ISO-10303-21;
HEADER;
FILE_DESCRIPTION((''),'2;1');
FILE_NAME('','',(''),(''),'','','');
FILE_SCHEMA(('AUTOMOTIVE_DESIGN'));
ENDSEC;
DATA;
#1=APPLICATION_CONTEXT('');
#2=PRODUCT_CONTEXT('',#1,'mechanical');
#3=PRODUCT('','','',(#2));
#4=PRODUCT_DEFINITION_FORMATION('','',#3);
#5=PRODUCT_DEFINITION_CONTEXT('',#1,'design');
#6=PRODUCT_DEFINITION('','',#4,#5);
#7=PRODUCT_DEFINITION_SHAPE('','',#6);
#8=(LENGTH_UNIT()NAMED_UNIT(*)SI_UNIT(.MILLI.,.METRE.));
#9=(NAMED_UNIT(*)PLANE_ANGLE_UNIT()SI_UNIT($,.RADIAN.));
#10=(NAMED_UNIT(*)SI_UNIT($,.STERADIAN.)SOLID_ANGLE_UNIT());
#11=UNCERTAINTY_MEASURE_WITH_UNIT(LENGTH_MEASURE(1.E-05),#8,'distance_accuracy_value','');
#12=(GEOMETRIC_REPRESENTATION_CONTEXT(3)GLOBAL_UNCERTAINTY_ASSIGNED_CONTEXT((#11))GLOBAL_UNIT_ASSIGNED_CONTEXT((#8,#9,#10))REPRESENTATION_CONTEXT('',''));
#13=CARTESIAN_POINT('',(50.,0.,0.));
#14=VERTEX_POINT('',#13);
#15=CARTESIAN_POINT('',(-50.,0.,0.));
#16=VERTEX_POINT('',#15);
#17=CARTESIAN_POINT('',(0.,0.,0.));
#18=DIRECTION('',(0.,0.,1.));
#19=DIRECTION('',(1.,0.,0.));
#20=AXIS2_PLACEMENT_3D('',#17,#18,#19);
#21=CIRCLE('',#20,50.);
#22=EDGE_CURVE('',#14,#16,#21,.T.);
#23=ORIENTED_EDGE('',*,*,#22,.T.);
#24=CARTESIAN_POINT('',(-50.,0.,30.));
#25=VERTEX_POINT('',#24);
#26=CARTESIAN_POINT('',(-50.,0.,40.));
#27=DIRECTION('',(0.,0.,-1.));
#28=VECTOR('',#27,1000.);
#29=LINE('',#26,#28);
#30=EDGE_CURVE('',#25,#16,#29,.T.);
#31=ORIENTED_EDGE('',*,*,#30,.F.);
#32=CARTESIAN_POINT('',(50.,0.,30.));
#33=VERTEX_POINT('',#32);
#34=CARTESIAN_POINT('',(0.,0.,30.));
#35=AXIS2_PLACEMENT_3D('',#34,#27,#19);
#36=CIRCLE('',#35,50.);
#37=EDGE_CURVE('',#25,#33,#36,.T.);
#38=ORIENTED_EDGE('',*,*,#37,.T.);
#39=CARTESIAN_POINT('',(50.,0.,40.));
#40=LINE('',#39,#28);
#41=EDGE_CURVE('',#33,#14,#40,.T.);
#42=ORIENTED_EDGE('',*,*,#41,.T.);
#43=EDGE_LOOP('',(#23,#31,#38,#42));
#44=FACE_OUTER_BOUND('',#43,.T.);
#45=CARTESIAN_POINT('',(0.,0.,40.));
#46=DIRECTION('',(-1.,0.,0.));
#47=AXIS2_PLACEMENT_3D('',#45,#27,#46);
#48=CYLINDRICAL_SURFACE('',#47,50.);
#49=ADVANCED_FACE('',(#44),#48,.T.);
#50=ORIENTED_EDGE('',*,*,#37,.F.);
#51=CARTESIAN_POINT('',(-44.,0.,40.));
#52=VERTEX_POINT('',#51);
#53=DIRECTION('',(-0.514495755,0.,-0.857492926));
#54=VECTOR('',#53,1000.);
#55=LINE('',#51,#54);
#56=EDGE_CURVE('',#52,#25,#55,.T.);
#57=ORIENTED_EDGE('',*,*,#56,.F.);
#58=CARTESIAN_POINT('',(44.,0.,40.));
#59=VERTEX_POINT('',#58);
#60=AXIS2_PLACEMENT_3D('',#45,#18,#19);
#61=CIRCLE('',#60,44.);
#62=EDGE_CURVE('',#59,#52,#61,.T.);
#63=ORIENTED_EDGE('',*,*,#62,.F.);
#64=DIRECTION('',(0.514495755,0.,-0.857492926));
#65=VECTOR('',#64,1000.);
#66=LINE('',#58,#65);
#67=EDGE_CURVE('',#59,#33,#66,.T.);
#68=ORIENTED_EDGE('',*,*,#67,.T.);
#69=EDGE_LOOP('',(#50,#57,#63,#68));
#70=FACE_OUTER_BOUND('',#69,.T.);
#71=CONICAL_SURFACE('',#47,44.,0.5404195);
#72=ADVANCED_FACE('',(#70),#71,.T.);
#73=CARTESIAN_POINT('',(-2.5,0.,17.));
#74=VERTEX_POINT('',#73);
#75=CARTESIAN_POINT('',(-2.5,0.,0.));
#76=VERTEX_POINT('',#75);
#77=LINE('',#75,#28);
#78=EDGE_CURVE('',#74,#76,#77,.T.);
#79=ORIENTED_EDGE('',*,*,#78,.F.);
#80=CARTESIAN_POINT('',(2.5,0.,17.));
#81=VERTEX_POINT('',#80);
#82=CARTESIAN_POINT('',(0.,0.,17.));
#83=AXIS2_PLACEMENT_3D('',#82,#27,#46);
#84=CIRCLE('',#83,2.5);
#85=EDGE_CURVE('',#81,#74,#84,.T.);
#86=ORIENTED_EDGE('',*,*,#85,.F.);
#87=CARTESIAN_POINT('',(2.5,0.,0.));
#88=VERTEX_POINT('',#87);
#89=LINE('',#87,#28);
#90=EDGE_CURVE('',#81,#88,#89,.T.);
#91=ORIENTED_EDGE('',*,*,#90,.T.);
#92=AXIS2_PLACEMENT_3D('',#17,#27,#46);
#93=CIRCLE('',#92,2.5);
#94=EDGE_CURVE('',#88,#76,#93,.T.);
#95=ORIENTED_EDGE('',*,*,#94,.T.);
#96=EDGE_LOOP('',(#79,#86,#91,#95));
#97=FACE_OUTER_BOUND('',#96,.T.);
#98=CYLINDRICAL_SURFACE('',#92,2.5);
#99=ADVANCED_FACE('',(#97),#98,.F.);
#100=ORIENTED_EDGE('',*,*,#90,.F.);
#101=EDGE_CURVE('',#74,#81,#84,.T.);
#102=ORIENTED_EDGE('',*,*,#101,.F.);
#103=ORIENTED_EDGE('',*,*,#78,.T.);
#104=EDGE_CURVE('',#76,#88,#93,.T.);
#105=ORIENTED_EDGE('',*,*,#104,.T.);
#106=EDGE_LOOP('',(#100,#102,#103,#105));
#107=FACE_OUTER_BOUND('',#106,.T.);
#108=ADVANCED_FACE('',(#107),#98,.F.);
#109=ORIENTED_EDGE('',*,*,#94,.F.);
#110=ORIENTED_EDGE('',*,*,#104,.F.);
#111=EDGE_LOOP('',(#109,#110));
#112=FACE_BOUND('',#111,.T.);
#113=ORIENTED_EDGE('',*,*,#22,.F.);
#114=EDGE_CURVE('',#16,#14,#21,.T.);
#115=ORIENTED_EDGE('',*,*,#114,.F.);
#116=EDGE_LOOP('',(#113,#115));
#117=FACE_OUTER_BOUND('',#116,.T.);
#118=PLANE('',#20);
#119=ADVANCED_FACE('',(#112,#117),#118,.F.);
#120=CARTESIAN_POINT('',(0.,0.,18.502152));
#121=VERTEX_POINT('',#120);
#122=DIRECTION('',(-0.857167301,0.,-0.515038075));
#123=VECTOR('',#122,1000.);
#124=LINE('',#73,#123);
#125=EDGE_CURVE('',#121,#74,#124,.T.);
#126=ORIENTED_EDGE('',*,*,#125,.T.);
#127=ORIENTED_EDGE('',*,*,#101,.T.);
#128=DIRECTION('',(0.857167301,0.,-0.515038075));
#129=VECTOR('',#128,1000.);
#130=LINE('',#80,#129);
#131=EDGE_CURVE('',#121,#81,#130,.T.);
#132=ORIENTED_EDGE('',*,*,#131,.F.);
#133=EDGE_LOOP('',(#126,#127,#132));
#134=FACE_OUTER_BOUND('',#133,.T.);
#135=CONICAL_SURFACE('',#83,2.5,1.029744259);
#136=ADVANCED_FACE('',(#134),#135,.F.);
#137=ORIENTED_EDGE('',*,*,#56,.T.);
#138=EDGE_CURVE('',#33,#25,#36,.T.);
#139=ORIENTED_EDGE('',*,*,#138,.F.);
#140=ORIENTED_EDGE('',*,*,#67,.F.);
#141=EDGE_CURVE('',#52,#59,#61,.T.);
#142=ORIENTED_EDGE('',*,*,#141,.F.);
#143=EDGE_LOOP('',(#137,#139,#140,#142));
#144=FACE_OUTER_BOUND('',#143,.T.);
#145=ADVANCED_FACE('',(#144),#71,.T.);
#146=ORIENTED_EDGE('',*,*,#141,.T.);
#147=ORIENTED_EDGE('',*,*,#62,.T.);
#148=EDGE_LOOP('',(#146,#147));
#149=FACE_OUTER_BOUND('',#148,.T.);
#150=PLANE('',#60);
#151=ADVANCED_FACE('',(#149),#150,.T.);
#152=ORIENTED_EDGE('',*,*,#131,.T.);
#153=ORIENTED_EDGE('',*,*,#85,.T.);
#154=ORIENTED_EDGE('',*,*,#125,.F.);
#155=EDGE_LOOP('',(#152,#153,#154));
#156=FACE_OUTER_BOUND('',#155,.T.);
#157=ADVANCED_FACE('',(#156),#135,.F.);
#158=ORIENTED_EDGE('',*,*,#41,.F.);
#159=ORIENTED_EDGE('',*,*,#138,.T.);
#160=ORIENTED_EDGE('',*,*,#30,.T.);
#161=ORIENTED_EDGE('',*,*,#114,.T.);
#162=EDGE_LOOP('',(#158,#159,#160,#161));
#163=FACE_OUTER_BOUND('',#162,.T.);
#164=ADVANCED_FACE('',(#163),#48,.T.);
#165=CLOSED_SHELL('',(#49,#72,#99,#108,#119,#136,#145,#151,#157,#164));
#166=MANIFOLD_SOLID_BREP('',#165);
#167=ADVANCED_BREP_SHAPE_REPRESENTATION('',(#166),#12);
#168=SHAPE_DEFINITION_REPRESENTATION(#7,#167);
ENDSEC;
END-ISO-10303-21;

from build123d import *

# Parameters (mm, degrees)
SKETCH1_R             = 50
BOSS_EXTRUDE1_DEPTH   = 40
CHAMFER1_SIZE         = 10
CHAMFER1_SIZE2        = 6
M6_TAPPED_HOLE1_D     = 5
M6_TAPPED_HOLE1_DEPTH = 17
M6_TAPPED_HOLE1_TIP   = 1.502151548


with BuildPart() as part:
    # Sketch1 → Boss-Extrude1 (new body)
    with BuildSketch(Plane.XY):
        Circle(SKETCH1_R)
    extrude(amount=BOSS_EXTRUDE1_DEPTH)

    # Chamfer1
    chamfer1_edges = [part.edges().sort_by_distance(p)[0] for p in [
        (-50, 0, 40),
    ]]
    chamfer1_side = [part.faces().sort_by_distance(p)[0] for p in [
        (-50, 0, 20),
    ]]
    chamfer(chamfer1_edges, length=CHAMFER1_SIZE, length2=CHAMFER1_SIZE2, reference=chamfer1_side[0])

    # M6 Tapped Hole1
    with Locations(Plane(origin=(0, 0, 0), x_dir=(-1, 0, 0), z_dir=(0, 0, -1))):
        with Locations((0, 0)):
            Hole(M6_TAPPED_HOLE1_D / 2, depth=M6_TAPPED_HOLE1_DEPTH)
            with Locations((0, 0, -(M6_TAPPED_HOLE1_DEPTH + M6_TAPPED_HOLE1_TIP / 2))):  # 118° drill point
                Cone(0, M6_TAPPED_HOLE1_D / 2, M6_TAPPED_HOLE1_TIP, mode=Mode.SUBTRACT)


solid = part.part
